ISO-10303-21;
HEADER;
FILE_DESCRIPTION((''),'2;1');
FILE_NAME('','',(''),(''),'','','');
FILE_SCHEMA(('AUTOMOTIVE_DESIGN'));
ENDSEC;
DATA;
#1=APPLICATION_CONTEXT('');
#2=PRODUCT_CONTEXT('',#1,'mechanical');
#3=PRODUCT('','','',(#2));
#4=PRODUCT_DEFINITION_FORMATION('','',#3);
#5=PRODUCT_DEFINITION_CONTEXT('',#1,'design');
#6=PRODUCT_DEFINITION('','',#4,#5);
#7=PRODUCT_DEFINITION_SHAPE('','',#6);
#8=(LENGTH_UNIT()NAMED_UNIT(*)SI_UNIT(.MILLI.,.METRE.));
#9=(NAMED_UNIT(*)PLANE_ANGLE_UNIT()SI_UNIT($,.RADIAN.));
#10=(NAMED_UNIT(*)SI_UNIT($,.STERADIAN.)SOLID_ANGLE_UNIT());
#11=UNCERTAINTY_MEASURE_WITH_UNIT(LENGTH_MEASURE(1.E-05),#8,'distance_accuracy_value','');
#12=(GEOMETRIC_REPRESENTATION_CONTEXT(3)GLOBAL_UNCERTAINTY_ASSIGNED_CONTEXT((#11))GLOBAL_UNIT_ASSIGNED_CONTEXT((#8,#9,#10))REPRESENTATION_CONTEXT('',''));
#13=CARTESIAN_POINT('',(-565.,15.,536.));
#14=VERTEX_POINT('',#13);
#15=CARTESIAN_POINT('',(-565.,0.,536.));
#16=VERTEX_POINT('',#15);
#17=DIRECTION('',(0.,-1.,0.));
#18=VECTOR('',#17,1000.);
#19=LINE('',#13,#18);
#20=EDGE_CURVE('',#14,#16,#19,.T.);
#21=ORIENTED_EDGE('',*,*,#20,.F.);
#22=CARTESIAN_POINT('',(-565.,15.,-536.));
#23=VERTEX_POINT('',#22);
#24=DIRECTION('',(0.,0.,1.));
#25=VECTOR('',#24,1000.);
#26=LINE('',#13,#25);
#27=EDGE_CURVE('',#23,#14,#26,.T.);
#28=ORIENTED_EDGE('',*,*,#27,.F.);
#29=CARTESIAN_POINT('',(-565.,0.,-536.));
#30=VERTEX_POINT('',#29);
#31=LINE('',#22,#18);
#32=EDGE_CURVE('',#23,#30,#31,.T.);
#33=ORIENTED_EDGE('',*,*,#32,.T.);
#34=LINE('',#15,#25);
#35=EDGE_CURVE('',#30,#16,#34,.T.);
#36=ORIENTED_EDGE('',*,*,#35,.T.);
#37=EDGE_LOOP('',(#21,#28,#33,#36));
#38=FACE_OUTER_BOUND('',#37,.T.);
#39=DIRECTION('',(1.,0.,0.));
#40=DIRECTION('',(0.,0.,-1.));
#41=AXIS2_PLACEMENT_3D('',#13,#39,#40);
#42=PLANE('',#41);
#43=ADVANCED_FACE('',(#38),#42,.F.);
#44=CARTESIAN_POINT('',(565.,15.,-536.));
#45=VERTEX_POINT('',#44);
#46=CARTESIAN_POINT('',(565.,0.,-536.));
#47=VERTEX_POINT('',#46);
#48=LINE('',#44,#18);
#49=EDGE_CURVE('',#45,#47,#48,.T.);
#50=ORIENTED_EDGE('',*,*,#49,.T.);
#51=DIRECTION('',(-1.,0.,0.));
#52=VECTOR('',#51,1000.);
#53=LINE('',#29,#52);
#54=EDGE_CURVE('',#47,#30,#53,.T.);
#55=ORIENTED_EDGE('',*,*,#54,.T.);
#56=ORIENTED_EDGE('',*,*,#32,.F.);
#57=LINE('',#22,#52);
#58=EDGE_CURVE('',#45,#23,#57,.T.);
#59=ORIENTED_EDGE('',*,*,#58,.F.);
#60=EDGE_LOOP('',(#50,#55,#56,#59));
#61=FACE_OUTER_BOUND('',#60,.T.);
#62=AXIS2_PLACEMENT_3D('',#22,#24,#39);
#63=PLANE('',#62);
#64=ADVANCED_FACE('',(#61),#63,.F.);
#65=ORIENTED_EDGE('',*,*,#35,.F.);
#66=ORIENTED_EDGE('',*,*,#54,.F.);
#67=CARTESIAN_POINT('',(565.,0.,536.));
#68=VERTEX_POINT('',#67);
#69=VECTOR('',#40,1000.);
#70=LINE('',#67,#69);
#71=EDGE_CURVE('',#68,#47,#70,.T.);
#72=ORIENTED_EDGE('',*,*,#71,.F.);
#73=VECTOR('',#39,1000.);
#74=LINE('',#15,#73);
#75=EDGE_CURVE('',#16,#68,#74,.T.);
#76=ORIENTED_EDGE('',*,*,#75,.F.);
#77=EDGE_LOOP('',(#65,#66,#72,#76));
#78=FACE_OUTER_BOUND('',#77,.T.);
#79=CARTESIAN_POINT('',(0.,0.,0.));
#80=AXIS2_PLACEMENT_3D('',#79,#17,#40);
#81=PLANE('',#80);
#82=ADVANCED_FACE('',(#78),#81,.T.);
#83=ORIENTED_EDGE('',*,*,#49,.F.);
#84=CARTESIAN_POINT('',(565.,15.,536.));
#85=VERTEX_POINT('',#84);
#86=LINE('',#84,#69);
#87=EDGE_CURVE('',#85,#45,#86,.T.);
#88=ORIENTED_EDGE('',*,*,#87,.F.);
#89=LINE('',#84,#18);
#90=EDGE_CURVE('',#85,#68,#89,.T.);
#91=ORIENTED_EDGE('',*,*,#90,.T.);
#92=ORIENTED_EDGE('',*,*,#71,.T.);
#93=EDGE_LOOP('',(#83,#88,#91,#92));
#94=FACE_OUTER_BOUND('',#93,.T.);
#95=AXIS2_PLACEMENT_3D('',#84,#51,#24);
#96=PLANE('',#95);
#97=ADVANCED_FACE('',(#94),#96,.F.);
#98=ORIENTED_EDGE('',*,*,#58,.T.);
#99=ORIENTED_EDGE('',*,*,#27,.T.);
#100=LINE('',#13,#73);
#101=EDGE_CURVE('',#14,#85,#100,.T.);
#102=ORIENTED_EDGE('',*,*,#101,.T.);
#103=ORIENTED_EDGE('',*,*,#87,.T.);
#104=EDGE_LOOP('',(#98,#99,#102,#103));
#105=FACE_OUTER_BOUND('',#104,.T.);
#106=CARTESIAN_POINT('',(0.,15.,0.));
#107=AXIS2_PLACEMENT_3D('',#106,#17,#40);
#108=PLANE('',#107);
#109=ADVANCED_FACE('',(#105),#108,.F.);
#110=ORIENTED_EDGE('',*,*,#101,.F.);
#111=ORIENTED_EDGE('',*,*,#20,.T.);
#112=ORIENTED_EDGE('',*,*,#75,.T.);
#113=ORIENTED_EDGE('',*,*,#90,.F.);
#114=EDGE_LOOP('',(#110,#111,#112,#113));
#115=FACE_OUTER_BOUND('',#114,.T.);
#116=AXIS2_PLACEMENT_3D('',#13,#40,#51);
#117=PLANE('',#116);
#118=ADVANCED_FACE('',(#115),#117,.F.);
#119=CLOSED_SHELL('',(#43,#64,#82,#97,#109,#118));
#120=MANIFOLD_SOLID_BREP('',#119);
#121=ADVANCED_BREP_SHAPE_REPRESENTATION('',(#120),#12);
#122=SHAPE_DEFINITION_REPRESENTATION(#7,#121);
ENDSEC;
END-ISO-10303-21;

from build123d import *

# Parameters (mm, degrees)
SKETCH_1_W      = 1130
SKETCH_1_H      = 1072
EXTRUDE_1_DEPTH = 15


with BuildPart() as part:
    # 草图1 → 凸台-拉伸1 (new body)
    with BuildSketch(Plane(origin=(0, 0, 0), x_dir=(1, 0, 0), z_dir=(0, 1, 0))):
        Rectangle(SKETCH_1_W, SKETCH_1_H)
    extrude(amount=EXTRUDE_1_DEPTH)


solid = part.part
